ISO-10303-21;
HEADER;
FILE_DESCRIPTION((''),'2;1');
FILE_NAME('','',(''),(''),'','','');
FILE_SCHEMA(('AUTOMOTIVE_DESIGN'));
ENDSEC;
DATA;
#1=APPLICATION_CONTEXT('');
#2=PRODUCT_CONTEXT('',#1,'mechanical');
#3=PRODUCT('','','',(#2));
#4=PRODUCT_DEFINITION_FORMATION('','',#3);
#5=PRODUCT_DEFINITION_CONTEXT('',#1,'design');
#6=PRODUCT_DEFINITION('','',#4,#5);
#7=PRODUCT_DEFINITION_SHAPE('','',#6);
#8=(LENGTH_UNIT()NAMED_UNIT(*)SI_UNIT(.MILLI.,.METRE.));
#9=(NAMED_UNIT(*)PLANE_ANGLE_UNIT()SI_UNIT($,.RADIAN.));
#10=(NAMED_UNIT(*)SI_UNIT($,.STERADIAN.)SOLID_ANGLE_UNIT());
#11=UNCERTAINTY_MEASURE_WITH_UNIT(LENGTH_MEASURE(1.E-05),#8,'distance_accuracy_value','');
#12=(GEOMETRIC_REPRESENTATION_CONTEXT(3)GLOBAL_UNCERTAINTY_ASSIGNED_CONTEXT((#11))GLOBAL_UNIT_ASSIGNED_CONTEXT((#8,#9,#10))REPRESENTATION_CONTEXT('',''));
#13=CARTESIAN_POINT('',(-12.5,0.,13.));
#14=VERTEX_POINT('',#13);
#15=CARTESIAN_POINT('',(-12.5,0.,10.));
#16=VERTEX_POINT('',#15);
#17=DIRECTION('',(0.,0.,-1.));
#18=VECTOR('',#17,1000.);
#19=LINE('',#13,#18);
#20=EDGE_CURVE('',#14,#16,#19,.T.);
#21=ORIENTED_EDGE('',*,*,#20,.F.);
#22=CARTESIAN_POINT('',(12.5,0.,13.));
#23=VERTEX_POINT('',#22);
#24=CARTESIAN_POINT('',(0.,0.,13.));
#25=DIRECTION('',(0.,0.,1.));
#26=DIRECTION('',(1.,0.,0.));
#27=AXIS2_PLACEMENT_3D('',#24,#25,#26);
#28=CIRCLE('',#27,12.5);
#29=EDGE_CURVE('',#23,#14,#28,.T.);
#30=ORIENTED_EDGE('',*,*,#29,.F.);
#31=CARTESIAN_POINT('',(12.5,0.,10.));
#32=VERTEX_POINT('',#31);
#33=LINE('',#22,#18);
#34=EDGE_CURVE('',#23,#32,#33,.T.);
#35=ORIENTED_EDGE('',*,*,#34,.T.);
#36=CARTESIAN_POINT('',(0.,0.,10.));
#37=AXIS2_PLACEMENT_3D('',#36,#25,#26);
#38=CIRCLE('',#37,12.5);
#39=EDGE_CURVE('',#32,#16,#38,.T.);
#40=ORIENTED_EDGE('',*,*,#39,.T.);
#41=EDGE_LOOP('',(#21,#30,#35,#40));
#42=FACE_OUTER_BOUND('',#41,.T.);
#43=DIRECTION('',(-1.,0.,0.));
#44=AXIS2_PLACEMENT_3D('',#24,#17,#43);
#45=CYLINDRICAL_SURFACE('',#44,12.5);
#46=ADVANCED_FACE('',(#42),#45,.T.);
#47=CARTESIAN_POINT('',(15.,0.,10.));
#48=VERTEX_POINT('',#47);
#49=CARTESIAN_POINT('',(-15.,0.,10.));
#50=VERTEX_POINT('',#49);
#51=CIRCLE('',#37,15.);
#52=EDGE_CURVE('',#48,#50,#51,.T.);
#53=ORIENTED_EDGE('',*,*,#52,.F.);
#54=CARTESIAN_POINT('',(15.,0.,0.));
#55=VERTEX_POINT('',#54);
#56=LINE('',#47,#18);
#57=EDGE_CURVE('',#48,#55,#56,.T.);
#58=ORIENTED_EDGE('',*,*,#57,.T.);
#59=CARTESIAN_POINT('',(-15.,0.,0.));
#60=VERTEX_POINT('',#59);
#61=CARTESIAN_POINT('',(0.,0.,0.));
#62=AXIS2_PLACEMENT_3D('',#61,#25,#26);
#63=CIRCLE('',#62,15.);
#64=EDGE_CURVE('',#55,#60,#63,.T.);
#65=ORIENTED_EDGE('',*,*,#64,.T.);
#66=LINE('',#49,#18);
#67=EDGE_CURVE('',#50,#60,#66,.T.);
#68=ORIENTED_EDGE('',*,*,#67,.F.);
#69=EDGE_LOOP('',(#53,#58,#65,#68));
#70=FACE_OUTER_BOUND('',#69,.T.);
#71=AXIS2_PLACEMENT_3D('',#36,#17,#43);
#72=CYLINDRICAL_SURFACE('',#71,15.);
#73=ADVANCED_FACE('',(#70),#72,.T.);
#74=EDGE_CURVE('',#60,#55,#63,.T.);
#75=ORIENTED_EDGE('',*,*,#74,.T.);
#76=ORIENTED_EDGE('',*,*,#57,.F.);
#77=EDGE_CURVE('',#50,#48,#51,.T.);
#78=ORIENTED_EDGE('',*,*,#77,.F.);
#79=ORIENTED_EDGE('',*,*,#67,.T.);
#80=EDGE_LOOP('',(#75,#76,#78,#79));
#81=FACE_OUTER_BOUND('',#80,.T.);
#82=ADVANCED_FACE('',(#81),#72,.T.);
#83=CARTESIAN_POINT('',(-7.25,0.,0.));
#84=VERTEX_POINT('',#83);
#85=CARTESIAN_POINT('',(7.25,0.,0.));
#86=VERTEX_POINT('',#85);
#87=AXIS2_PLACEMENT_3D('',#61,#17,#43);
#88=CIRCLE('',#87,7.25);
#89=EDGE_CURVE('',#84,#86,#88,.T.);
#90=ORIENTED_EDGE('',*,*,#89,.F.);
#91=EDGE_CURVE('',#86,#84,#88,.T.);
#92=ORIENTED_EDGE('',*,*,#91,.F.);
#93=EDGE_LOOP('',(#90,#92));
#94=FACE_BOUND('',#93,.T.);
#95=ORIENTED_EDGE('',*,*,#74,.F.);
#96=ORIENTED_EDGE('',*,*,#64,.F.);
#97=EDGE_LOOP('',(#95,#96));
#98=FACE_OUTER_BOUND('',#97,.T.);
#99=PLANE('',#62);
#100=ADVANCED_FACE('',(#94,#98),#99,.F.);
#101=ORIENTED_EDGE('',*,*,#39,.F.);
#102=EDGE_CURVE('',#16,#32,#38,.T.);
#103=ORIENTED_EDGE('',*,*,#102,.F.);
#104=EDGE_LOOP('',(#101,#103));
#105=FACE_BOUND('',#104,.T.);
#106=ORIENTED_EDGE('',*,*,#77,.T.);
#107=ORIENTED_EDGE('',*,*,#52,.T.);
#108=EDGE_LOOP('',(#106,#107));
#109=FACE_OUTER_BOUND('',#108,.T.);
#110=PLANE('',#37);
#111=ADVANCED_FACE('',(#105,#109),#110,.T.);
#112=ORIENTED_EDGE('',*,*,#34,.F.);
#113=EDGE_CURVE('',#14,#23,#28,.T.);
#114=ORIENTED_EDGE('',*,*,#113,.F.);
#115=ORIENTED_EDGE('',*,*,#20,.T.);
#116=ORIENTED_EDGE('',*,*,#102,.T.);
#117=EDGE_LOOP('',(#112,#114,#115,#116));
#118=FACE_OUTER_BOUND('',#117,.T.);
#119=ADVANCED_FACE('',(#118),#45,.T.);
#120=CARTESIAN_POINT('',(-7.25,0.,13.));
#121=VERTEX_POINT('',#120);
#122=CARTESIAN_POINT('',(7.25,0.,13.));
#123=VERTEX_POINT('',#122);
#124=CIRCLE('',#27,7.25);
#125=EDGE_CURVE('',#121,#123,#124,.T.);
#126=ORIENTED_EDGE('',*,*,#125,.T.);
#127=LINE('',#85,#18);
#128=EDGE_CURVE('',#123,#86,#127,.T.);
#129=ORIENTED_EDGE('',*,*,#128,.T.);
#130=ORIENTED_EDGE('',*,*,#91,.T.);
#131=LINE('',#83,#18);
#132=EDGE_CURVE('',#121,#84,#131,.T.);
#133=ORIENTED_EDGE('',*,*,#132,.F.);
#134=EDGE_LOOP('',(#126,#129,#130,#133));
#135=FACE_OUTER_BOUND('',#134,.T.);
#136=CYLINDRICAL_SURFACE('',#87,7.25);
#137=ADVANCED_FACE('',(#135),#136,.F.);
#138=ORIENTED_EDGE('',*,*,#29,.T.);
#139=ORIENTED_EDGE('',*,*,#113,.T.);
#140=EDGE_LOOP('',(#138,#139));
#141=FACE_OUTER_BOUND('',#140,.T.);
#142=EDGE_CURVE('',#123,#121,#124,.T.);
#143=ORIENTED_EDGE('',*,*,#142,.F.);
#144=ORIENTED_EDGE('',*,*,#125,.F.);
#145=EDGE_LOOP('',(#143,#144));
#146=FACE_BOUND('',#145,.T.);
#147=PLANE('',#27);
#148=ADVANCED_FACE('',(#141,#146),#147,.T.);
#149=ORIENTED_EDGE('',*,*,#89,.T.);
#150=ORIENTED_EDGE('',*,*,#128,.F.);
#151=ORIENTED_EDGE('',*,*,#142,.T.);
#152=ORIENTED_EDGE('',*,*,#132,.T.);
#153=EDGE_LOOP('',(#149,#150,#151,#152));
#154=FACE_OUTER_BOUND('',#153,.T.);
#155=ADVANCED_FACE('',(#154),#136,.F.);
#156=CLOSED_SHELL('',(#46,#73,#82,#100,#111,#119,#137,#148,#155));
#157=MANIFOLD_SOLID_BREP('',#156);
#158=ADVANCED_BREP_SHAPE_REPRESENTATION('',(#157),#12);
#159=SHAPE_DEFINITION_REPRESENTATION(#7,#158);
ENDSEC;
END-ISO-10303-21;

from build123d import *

# Parameters (mm, degrees)
SKETCH1_R                  = 15
BOSS_EXTRUDE1_DEPTH        = 10
SKETCH2_R                  = 12.5
BOSS_EXTRUDE2_DEPTH        = 3
SKETCH3_R                  = 6
CUT_EXTRUDE1_DEPTH         = 25.879710609
M16X1_5_TAPPED_HOLE1_D     = 14.5
M16X1_5_TAPPED_HOLE1_DEPTH = 39.5
M16X1_5_TAPPED_HOLE1_TIP   = 4.356239488


with BuildPart() as part:
    # Sketch1 → Boss-Extrude1 (new body)
    with BuildSketch(Plane.XY):
        Circle(SKETCH1_R)
    extrude(amount=BOSS_EXTRUDE1_DEPTH)

    # Sketch2 → Boss-Extrude2 (add)
    with BuildSketch(Plane.XY.offset(10)):
        Circle(SKETCH2_R)
    extrude(amount=BOSS_EXTRUDE2_DEPTH)

    # Sketch3 → Cut-Extrude1 (cut, through all)
    with BuildSketch(Plane.XY.offset(13)):
        Circle(SKETCH3_R)
    extrude(amount=-CUT_EXTRUDE1_DEPTH, mode=Mode.SUBTRACT)

    # M16x1.5 Tapped Hole1
    with Locations(Plane(origin=(0, 0, 0), x_dir=(-1, 0, 0), z_dir=(0, 0, -1))):
        with Locations((0, 0)):
            Hole(M16X1_5_TAPPED_HOLE1_D / 2, depth=M16X1_5_TAPPED_HOLE1_DEPTH)
            with Locations((0, 0, -(M16X1_5_TAPPED_HOLE1_DEPTH + M16X1_5_TAPPED_HOLE1_TIP / 2))):  # 118° drill point
                Cone(0, M16X1_5_TAPPED_HOLE1_D / 2, M16X1_5_TAPPED_HOLE1_TIP, mode=Mode.SUBTRACT)


solid = part.part
